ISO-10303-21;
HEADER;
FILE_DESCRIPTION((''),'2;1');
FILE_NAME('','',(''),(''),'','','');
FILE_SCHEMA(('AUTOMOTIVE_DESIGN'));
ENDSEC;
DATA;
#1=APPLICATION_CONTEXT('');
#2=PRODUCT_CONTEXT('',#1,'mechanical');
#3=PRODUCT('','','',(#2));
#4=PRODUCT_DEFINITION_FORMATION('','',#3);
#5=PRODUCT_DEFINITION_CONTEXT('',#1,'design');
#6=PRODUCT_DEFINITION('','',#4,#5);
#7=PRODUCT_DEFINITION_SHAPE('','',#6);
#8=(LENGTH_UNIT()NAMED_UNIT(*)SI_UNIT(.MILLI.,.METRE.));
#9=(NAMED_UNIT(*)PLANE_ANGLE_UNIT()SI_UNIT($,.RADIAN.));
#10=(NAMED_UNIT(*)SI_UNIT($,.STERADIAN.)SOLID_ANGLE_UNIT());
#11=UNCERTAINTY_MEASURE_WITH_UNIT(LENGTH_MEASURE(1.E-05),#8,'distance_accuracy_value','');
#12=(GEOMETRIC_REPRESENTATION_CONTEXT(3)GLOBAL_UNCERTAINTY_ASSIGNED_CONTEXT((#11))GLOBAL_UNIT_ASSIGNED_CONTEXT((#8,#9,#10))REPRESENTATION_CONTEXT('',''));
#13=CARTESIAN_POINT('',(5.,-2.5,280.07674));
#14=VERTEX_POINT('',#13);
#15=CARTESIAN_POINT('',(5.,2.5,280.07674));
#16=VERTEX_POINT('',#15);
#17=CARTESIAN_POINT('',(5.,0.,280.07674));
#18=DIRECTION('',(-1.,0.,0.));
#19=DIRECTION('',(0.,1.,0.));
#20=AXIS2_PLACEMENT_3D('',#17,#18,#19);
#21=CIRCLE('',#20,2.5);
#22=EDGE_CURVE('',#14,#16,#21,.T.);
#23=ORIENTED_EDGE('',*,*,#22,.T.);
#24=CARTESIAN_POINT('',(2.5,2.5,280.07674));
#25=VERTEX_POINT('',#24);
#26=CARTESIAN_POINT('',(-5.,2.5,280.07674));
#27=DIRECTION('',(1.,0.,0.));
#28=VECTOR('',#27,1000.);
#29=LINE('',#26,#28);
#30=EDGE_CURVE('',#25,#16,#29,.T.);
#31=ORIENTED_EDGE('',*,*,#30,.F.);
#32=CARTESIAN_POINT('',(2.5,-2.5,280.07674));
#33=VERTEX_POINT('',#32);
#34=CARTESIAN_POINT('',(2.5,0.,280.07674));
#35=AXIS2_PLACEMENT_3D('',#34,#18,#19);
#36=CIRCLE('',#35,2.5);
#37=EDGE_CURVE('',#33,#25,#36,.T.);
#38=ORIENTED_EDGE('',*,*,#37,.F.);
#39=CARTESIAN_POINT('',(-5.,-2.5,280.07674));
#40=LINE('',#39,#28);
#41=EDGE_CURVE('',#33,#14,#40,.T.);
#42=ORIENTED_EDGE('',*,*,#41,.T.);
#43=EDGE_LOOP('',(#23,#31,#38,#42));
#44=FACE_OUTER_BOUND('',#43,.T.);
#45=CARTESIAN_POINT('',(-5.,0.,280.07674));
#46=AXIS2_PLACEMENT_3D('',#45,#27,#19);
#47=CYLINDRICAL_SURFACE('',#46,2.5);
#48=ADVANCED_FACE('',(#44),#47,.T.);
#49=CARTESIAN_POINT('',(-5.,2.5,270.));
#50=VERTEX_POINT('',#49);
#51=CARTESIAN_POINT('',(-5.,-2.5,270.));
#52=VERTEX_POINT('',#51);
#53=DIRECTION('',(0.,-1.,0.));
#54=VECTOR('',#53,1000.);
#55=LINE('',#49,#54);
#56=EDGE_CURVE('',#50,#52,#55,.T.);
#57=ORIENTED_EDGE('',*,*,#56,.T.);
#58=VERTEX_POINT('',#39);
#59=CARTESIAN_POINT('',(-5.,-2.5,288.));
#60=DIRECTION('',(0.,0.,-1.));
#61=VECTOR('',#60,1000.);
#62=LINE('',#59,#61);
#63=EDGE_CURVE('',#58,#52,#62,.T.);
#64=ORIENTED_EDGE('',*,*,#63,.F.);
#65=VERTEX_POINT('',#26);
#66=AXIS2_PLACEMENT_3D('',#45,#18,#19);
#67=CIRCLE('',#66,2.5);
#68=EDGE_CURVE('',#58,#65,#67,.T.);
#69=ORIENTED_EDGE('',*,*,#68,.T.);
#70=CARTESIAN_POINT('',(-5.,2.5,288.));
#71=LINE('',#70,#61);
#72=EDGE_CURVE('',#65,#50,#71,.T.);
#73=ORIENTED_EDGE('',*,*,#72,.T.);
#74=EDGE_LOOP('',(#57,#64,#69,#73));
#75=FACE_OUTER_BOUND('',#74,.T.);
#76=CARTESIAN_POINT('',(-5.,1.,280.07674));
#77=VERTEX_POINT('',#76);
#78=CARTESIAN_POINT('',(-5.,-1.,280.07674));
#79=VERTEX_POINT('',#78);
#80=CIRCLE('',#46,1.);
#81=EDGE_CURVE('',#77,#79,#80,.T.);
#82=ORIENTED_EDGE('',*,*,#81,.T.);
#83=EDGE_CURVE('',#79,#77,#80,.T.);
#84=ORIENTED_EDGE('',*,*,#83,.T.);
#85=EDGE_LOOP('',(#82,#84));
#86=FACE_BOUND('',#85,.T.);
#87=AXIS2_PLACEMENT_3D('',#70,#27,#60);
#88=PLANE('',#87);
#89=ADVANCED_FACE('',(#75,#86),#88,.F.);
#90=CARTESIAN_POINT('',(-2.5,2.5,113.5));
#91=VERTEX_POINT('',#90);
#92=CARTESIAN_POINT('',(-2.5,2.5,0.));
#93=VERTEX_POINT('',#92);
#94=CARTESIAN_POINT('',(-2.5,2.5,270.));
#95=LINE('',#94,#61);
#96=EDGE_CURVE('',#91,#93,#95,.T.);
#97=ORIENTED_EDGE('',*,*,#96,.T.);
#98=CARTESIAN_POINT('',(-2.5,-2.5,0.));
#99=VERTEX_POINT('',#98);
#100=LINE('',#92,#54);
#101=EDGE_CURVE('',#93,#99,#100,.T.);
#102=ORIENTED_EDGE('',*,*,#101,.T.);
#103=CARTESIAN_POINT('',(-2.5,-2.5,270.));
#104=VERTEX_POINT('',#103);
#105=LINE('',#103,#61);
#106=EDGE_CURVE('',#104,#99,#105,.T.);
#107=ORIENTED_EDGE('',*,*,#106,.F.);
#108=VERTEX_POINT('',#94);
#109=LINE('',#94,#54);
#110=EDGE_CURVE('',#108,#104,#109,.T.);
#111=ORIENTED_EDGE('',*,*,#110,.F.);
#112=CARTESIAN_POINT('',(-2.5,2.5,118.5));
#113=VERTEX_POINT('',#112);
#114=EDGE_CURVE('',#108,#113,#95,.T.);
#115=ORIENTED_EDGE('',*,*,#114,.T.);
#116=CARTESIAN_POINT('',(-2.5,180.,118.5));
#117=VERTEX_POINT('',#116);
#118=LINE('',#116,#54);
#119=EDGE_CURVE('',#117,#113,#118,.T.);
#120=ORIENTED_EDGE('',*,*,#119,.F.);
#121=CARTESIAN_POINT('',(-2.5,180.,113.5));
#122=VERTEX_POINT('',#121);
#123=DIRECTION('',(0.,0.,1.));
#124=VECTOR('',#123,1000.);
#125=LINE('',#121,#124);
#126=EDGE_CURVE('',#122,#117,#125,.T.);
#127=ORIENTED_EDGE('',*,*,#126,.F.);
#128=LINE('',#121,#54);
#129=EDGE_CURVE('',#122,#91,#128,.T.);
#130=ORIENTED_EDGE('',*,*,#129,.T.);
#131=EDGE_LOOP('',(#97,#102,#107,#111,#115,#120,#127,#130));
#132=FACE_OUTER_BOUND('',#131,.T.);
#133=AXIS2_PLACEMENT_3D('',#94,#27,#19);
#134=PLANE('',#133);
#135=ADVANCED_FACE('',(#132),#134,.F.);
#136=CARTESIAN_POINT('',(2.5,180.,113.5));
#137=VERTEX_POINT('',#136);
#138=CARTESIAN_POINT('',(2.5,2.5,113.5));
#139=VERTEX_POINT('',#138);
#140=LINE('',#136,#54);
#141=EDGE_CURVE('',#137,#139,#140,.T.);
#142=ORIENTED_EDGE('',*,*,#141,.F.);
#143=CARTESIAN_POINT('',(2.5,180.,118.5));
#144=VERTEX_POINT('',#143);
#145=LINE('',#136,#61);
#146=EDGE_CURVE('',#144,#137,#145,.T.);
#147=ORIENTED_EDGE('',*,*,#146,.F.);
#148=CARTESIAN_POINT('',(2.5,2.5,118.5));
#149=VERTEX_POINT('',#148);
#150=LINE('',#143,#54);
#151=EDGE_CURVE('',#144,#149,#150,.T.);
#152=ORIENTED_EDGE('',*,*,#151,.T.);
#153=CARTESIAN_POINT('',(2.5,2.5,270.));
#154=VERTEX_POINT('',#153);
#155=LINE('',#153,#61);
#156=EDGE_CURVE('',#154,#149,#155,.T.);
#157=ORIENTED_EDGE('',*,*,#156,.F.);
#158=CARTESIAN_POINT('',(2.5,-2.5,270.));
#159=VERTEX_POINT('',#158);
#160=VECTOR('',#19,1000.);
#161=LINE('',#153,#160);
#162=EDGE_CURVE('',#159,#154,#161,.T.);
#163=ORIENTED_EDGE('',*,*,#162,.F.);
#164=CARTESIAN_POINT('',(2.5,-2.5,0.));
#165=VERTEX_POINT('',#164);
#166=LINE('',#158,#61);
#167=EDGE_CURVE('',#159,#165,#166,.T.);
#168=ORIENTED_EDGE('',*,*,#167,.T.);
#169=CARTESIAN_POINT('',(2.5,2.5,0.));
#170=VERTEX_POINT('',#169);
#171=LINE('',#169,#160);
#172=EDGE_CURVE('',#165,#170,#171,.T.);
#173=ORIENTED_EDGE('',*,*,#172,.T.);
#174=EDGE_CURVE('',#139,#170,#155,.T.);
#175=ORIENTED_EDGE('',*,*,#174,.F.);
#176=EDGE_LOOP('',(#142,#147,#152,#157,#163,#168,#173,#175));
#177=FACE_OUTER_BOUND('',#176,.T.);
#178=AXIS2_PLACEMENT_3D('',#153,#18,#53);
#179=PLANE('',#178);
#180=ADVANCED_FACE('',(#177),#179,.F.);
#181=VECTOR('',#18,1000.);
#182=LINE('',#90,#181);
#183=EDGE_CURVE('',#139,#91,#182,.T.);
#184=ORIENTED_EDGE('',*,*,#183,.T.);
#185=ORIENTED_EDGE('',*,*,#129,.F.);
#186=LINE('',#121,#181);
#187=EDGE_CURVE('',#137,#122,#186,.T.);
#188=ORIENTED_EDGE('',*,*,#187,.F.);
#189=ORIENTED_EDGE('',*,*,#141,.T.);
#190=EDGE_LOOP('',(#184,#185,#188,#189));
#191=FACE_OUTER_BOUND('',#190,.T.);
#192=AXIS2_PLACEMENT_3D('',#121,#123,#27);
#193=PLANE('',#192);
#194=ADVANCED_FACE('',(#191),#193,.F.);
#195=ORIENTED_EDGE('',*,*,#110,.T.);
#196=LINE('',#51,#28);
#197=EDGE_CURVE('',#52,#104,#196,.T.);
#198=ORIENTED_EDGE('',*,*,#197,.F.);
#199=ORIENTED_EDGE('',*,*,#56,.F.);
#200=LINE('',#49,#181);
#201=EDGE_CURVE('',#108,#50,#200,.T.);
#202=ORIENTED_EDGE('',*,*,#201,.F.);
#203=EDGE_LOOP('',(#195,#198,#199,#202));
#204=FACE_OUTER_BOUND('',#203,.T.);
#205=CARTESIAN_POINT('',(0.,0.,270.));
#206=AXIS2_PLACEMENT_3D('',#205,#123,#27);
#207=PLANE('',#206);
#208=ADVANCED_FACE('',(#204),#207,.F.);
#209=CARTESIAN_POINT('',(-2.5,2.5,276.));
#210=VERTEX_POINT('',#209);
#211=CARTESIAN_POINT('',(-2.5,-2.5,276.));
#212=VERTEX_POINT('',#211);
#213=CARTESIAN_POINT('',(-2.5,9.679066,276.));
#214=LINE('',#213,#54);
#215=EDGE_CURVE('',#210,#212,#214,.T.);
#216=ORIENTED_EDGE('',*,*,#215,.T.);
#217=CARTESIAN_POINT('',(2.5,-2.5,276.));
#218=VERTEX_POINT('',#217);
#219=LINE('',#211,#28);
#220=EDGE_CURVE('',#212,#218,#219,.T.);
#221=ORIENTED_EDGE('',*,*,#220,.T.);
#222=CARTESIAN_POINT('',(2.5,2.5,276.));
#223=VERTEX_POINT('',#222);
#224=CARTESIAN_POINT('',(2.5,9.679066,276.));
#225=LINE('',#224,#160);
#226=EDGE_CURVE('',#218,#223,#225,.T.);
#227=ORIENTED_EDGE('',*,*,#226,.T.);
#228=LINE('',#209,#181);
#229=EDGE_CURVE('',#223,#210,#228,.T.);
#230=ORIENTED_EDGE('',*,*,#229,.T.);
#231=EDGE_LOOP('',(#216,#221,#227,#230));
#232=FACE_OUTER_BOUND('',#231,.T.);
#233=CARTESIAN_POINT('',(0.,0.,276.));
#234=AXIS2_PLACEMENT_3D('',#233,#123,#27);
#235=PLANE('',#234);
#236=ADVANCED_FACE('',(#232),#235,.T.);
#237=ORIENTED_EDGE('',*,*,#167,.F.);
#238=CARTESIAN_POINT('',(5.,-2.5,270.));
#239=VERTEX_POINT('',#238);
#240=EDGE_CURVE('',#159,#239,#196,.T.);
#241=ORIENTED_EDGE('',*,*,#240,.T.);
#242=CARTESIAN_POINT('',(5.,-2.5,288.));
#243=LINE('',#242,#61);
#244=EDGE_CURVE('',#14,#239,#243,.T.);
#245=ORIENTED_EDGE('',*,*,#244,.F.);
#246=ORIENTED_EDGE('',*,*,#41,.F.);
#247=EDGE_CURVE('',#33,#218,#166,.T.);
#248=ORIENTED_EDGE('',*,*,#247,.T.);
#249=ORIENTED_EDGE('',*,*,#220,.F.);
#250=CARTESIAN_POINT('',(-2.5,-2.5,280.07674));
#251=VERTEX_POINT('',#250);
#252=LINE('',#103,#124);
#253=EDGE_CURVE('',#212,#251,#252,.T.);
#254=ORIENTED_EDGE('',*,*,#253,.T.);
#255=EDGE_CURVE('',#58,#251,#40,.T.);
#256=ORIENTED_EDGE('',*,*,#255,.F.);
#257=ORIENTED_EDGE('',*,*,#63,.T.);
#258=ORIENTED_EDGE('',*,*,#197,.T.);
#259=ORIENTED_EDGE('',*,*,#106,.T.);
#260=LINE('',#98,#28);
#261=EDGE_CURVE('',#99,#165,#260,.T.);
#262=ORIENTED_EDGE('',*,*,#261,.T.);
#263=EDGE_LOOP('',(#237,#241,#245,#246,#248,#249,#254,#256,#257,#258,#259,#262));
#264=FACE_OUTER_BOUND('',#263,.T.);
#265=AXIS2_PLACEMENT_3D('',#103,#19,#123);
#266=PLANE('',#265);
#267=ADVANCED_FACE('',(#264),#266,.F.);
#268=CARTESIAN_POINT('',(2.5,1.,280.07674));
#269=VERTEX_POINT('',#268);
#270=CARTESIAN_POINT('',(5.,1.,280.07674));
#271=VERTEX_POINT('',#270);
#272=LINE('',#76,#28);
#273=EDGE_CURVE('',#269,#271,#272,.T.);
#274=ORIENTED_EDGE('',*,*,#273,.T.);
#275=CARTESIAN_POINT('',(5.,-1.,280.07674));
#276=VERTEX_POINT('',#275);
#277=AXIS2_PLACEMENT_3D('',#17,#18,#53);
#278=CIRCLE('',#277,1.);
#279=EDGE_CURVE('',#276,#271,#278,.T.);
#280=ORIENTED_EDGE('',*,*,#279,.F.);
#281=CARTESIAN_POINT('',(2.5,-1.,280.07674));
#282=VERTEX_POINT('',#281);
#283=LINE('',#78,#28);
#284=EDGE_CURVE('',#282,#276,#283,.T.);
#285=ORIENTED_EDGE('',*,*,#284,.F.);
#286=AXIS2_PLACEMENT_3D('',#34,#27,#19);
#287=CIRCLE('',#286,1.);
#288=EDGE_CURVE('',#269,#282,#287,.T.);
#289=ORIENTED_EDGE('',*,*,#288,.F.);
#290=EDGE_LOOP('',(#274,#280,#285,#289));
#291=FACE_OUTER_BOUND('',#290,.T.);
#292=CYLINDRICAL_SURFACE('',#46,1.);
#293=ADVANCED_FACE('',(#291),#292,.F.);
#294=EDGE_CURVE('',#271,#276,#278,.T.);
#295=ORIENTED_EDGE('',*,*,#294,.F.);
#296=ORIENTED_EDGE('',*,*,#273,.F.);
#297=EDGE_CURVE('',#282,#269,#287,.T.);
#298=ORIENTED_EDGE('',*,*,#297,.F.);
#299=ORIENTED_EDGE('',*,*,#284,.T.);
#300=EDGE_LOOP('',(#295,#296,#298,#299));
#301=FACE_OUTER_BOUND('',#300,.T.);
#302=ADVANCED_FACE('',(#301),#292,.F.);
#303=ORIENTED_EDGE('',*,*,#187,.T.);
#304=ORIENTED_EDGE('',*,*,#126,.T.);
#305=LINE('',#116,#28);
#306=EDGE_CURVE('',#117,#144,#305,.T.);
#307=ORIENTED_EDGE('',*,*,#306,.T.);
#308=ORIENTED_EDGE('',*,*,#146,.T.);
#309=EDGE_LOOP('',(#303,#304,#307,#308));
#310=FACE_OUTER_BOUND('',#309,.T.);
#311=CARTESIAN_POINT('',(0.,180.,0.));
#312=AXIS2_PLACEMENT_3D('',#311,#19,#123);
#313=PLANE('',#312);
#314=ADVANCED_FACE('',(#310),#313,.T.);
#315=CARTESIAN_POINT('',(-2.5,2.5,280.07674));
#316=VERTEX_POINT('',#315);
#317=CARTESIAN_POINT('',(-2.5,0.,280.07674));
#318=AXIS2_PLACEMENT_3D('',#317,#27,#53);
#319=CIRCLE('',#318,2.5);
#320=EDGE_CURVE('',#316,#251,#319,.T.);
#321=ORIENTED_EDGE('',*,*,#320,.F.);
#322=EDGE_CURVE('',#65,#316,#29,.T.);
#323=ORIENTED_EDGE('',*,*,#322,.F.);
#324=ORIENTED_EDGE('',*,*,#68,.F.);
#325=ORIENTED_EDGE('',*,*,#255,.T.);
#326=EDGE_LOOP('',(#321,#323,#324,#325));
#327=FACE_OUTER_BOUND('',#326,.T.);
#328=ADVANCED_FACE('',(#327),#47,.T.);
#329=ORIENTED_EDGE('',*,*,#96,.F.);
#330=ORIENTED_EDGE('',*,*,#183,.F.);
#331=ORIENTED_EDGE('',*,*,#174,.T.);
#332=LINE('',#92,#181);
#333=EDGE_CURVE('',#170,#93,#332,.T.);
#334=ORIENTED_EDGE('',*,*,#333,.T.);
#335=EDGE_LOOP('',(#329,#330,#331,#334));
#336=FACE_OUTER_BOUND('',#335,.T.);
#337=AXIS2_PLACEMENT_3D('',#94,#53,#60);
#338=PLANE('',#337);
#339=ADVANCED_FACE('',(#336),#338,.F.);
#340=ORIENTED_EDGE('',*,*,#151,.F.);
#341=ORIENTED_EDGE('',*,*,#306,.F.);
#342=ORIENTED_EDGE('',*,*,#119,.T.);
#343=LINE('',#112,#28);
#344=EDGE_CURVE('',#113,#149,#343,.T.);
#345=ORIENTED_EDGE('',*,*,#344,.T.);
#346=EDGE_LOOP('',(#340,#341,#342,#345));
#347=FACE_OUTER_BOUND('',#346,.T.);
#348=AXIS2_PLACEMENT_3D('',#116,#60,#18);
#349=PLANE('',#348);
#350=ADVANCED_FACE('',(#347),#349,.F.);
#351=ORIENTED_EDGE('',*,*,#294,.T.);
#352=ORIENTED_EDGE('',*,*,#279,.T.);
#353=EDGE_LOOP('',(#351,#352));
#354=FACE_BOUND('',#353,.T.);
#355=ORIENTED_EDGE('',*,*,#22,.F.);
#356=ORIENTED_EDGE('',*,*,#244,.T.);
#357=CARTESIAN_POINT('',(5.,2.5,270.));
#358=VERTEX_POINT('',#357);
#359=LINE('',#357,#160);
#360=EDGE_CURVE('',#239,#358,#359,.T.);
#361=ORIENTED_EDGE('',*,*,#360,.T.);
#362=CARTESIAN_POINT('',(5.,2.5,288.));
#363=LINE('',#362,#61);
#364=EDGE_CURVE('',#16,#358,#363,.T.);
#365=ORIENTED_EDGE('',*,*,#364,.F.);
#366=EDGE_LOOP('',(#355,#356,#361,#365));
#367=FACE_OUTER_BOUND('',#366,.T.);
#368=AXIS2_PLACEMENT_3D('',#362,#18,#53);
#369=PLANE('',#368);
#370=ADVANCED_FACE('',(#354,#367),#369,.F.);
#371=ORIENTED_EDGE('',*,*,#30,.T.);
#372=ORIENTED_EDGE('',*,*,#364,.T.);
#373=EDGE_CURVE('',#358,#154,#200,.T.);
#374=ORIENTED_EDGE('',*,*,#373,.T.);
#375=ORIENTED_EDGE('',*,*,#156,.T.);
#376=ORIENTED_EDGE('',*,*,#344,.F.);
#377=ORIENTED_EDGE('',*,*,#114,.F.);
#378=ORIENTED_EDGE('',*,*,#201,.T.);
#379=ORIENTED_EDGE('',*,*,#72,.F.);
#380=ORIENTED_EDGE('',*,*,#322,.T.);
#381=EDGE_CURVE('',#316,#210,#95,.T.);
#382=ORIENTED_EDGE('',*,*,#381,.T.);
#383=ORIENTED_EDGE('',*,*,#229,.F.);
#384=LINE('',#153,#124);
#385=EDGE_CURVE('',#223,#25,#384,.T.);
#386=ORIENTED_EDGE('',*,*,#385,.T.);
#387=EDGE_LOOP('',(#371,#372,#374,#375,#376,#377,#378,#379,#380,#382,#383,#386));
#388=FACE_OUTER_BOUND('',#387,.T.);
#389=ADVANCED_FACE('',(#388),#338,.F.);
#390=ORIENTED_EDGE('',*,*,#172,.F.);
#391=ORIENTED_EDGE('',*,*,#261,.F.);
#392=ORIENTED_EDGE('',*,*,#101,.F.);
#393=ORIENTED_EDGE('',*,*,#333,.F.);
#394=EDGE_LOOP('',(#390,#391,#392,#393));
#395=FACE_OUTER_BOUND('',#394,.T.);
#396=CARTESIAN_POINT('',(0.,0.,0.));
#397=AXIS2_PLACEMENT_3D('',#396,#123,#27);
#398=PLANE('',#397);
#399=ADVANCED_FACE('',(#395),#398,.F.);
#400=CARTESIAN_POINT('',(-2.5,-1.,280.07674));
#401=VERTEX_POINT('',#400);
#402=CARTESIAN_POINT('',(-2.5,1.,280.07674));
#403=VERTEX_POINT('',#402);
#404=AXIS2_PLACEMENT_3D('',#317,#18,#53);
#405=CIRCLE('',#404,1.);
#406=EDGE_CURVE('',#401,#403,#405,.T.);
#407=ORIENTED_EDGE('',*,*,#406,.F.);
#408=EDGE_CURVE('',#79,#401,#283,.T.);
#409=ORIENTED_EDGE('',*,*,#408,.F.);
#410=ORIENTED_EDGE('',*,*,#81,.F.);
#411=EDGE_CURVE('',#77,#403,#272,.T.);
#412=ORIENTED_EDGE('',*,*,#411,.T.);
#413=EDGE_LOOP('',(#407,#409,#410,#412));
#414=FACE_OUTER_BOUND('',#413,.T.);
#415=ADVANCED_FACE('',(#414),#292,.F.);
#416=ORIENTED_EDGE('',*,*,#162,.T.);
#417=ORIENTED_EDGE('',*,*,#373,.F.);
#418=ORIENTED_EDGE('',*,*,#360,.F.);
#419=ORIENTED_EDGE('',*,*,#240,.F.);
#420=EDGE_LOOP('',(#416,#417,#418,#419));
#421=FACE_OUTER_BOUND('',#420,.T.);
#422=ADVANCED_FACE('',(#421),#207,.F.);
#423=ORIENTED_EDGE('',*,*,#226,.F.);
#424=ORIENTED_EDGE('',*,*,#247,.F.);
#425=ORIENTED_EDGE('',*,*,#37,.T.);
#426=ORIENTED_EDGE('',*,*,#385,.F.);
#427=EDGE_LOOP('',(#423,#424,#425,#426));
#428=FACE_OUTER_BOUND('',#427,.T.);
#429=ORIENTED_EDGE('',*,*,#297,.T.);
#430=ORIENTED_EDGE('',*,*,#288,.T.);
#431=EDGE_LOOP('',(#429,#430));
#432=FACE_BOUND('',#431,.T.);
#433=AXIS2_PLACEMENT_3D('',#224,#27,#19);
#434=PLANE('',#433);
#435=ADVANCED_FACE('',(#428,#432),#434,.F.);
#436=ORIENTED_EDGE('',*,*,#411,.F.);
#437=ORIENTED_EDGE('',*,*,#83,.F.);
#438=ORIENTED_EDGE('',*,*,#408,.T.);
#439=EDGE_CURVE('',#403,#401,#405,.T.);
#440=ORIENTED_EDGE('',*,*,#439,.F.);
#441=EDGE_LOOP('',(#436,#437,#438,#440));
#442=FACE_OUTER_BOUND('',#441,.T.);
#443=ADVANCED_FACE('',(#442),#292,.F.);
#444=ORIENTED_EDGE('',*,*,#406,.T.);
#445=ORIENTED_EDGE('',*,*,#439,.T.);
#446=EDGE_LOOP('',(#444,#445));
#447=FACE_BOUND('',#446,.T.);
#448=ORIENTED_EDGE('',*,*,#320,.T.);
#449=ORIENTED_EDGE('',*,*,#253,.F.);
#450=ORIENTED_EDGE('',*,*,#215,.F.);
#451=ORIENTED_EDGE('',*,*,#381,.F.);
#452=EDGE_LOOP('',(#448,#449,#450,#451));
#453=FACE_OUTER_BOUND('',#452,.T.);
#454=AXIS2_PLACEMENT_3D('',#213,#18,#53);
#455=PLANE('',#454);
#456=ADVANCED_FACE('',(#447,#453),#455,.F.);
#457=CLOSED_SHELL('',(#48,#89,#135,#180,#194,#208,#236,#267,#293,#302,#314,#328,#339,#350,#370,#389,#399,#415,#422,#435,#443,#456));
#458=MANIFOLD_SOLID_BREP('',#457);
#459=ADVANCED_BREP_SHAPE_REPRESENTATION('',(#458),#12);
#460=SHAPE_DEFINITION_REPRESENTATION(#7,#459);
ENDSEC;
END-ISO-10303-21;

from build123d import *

# Parameters (mm, degrees)
SKETCH1_W               = 5
SKETCH1_H               = 5
BOSS_EXTRUDE1_DEPTH     = 270
SKETCH2_W               = 10
SKETCH2_H               = 5
BOSS_EXTRUDE2_DEPTH     = 18
SKETCH3_W               = 5
SKETCH3_H               = 19.358131828
CUT_EXTRUDE1_DEPTH      = 12
CUT_EXTRUDE2_DEPTH      = 289.18440277
CUT_EXTRUDE2_DEPTH_BACK = 289.18440277
SKETCH4_R               = 1
SKETCH5_W               = 5
SKETCH5_H               = 5
BOSS_EXTRUDE3_DEPTH     = 180


with BuildPart() as part:
    # Sketch1 → Boss-Extrude1 (new body)
    with BuildSketch(Plane.XY):
        Rectangle(SKETCH1_W, SKETCH1_H)
    extrude(amount=BOSS_EXTRUDE1_DEPTH)

    # Sketch2 → Boss-Extrude2 (add)
    with BuildSketch(Plane.XY.offset(270)):
        Rectangle(SKETCH2_W, SKETCH2_H)
    extrude(amount=BOSS_EXTRUDE2_DEPTH)

    # Sketch3 → Cut-Extrude1 (cut)
    with BuildSketch(Plane.XY.offset(288)):
        Rectangle(SKETCH3_W, SKETCH3_H)
    extrude(amount=-CUT_EXTRUDE1_DEPTH, mode=Mode.SUBTRACT)

    # Sketch4 → Cut-Extrude2 (cut, two sides: drawn at the far end of the back side and taken through both)
    with BuildSketch(Plane(origin=(5, 0, 0), x_dir=(0, 0, -1), z_dir=(1, 0, 0)).offset(-CUT_EXTRUDE2_DEPTH_BACK)):
        with Locations(Location((-280.07674021, 0, 0), (0, 0, 90))):
            Circle(SKETCH4_R)
        with BuildLine():
            Line((-280.07674021, 2.5), (-280.07674021, 12.098504892))
            Line((-280.07674021, 12.098504892), (-285.8811548, 12.098504892))
            Line((-285.8811548, 12.098504892), (-318.827178265, -19.142217328))
            Line((-318.827178265, -19.142217328), (-280.07674021, -2.5))
            ThreePointArc((-280.07674021, -2.5), (-282.57674021, 0), (-280.07674021, 2.5))
        make_face()
    extrude(amount=CUT_EXTRUDE2_DEPTH + CUT_EXTRUDE2_DEPTH_BACK, mode=Mode.SUBTRACT)

    # Sketch5 → Boss-Extrude3 (add)
    with BuildSketch(Plane(origin=(0, 0, 0), x_dir=(1, 0, 0), z_dir=(0, 1, 0))):
        with Locations((0, -116)):
            Rectangle(SKETCH5_W, SKETCH5_H)
    extrude(amount=BOSS_EXTRUDE3_DEPTH)


solid = part.part
